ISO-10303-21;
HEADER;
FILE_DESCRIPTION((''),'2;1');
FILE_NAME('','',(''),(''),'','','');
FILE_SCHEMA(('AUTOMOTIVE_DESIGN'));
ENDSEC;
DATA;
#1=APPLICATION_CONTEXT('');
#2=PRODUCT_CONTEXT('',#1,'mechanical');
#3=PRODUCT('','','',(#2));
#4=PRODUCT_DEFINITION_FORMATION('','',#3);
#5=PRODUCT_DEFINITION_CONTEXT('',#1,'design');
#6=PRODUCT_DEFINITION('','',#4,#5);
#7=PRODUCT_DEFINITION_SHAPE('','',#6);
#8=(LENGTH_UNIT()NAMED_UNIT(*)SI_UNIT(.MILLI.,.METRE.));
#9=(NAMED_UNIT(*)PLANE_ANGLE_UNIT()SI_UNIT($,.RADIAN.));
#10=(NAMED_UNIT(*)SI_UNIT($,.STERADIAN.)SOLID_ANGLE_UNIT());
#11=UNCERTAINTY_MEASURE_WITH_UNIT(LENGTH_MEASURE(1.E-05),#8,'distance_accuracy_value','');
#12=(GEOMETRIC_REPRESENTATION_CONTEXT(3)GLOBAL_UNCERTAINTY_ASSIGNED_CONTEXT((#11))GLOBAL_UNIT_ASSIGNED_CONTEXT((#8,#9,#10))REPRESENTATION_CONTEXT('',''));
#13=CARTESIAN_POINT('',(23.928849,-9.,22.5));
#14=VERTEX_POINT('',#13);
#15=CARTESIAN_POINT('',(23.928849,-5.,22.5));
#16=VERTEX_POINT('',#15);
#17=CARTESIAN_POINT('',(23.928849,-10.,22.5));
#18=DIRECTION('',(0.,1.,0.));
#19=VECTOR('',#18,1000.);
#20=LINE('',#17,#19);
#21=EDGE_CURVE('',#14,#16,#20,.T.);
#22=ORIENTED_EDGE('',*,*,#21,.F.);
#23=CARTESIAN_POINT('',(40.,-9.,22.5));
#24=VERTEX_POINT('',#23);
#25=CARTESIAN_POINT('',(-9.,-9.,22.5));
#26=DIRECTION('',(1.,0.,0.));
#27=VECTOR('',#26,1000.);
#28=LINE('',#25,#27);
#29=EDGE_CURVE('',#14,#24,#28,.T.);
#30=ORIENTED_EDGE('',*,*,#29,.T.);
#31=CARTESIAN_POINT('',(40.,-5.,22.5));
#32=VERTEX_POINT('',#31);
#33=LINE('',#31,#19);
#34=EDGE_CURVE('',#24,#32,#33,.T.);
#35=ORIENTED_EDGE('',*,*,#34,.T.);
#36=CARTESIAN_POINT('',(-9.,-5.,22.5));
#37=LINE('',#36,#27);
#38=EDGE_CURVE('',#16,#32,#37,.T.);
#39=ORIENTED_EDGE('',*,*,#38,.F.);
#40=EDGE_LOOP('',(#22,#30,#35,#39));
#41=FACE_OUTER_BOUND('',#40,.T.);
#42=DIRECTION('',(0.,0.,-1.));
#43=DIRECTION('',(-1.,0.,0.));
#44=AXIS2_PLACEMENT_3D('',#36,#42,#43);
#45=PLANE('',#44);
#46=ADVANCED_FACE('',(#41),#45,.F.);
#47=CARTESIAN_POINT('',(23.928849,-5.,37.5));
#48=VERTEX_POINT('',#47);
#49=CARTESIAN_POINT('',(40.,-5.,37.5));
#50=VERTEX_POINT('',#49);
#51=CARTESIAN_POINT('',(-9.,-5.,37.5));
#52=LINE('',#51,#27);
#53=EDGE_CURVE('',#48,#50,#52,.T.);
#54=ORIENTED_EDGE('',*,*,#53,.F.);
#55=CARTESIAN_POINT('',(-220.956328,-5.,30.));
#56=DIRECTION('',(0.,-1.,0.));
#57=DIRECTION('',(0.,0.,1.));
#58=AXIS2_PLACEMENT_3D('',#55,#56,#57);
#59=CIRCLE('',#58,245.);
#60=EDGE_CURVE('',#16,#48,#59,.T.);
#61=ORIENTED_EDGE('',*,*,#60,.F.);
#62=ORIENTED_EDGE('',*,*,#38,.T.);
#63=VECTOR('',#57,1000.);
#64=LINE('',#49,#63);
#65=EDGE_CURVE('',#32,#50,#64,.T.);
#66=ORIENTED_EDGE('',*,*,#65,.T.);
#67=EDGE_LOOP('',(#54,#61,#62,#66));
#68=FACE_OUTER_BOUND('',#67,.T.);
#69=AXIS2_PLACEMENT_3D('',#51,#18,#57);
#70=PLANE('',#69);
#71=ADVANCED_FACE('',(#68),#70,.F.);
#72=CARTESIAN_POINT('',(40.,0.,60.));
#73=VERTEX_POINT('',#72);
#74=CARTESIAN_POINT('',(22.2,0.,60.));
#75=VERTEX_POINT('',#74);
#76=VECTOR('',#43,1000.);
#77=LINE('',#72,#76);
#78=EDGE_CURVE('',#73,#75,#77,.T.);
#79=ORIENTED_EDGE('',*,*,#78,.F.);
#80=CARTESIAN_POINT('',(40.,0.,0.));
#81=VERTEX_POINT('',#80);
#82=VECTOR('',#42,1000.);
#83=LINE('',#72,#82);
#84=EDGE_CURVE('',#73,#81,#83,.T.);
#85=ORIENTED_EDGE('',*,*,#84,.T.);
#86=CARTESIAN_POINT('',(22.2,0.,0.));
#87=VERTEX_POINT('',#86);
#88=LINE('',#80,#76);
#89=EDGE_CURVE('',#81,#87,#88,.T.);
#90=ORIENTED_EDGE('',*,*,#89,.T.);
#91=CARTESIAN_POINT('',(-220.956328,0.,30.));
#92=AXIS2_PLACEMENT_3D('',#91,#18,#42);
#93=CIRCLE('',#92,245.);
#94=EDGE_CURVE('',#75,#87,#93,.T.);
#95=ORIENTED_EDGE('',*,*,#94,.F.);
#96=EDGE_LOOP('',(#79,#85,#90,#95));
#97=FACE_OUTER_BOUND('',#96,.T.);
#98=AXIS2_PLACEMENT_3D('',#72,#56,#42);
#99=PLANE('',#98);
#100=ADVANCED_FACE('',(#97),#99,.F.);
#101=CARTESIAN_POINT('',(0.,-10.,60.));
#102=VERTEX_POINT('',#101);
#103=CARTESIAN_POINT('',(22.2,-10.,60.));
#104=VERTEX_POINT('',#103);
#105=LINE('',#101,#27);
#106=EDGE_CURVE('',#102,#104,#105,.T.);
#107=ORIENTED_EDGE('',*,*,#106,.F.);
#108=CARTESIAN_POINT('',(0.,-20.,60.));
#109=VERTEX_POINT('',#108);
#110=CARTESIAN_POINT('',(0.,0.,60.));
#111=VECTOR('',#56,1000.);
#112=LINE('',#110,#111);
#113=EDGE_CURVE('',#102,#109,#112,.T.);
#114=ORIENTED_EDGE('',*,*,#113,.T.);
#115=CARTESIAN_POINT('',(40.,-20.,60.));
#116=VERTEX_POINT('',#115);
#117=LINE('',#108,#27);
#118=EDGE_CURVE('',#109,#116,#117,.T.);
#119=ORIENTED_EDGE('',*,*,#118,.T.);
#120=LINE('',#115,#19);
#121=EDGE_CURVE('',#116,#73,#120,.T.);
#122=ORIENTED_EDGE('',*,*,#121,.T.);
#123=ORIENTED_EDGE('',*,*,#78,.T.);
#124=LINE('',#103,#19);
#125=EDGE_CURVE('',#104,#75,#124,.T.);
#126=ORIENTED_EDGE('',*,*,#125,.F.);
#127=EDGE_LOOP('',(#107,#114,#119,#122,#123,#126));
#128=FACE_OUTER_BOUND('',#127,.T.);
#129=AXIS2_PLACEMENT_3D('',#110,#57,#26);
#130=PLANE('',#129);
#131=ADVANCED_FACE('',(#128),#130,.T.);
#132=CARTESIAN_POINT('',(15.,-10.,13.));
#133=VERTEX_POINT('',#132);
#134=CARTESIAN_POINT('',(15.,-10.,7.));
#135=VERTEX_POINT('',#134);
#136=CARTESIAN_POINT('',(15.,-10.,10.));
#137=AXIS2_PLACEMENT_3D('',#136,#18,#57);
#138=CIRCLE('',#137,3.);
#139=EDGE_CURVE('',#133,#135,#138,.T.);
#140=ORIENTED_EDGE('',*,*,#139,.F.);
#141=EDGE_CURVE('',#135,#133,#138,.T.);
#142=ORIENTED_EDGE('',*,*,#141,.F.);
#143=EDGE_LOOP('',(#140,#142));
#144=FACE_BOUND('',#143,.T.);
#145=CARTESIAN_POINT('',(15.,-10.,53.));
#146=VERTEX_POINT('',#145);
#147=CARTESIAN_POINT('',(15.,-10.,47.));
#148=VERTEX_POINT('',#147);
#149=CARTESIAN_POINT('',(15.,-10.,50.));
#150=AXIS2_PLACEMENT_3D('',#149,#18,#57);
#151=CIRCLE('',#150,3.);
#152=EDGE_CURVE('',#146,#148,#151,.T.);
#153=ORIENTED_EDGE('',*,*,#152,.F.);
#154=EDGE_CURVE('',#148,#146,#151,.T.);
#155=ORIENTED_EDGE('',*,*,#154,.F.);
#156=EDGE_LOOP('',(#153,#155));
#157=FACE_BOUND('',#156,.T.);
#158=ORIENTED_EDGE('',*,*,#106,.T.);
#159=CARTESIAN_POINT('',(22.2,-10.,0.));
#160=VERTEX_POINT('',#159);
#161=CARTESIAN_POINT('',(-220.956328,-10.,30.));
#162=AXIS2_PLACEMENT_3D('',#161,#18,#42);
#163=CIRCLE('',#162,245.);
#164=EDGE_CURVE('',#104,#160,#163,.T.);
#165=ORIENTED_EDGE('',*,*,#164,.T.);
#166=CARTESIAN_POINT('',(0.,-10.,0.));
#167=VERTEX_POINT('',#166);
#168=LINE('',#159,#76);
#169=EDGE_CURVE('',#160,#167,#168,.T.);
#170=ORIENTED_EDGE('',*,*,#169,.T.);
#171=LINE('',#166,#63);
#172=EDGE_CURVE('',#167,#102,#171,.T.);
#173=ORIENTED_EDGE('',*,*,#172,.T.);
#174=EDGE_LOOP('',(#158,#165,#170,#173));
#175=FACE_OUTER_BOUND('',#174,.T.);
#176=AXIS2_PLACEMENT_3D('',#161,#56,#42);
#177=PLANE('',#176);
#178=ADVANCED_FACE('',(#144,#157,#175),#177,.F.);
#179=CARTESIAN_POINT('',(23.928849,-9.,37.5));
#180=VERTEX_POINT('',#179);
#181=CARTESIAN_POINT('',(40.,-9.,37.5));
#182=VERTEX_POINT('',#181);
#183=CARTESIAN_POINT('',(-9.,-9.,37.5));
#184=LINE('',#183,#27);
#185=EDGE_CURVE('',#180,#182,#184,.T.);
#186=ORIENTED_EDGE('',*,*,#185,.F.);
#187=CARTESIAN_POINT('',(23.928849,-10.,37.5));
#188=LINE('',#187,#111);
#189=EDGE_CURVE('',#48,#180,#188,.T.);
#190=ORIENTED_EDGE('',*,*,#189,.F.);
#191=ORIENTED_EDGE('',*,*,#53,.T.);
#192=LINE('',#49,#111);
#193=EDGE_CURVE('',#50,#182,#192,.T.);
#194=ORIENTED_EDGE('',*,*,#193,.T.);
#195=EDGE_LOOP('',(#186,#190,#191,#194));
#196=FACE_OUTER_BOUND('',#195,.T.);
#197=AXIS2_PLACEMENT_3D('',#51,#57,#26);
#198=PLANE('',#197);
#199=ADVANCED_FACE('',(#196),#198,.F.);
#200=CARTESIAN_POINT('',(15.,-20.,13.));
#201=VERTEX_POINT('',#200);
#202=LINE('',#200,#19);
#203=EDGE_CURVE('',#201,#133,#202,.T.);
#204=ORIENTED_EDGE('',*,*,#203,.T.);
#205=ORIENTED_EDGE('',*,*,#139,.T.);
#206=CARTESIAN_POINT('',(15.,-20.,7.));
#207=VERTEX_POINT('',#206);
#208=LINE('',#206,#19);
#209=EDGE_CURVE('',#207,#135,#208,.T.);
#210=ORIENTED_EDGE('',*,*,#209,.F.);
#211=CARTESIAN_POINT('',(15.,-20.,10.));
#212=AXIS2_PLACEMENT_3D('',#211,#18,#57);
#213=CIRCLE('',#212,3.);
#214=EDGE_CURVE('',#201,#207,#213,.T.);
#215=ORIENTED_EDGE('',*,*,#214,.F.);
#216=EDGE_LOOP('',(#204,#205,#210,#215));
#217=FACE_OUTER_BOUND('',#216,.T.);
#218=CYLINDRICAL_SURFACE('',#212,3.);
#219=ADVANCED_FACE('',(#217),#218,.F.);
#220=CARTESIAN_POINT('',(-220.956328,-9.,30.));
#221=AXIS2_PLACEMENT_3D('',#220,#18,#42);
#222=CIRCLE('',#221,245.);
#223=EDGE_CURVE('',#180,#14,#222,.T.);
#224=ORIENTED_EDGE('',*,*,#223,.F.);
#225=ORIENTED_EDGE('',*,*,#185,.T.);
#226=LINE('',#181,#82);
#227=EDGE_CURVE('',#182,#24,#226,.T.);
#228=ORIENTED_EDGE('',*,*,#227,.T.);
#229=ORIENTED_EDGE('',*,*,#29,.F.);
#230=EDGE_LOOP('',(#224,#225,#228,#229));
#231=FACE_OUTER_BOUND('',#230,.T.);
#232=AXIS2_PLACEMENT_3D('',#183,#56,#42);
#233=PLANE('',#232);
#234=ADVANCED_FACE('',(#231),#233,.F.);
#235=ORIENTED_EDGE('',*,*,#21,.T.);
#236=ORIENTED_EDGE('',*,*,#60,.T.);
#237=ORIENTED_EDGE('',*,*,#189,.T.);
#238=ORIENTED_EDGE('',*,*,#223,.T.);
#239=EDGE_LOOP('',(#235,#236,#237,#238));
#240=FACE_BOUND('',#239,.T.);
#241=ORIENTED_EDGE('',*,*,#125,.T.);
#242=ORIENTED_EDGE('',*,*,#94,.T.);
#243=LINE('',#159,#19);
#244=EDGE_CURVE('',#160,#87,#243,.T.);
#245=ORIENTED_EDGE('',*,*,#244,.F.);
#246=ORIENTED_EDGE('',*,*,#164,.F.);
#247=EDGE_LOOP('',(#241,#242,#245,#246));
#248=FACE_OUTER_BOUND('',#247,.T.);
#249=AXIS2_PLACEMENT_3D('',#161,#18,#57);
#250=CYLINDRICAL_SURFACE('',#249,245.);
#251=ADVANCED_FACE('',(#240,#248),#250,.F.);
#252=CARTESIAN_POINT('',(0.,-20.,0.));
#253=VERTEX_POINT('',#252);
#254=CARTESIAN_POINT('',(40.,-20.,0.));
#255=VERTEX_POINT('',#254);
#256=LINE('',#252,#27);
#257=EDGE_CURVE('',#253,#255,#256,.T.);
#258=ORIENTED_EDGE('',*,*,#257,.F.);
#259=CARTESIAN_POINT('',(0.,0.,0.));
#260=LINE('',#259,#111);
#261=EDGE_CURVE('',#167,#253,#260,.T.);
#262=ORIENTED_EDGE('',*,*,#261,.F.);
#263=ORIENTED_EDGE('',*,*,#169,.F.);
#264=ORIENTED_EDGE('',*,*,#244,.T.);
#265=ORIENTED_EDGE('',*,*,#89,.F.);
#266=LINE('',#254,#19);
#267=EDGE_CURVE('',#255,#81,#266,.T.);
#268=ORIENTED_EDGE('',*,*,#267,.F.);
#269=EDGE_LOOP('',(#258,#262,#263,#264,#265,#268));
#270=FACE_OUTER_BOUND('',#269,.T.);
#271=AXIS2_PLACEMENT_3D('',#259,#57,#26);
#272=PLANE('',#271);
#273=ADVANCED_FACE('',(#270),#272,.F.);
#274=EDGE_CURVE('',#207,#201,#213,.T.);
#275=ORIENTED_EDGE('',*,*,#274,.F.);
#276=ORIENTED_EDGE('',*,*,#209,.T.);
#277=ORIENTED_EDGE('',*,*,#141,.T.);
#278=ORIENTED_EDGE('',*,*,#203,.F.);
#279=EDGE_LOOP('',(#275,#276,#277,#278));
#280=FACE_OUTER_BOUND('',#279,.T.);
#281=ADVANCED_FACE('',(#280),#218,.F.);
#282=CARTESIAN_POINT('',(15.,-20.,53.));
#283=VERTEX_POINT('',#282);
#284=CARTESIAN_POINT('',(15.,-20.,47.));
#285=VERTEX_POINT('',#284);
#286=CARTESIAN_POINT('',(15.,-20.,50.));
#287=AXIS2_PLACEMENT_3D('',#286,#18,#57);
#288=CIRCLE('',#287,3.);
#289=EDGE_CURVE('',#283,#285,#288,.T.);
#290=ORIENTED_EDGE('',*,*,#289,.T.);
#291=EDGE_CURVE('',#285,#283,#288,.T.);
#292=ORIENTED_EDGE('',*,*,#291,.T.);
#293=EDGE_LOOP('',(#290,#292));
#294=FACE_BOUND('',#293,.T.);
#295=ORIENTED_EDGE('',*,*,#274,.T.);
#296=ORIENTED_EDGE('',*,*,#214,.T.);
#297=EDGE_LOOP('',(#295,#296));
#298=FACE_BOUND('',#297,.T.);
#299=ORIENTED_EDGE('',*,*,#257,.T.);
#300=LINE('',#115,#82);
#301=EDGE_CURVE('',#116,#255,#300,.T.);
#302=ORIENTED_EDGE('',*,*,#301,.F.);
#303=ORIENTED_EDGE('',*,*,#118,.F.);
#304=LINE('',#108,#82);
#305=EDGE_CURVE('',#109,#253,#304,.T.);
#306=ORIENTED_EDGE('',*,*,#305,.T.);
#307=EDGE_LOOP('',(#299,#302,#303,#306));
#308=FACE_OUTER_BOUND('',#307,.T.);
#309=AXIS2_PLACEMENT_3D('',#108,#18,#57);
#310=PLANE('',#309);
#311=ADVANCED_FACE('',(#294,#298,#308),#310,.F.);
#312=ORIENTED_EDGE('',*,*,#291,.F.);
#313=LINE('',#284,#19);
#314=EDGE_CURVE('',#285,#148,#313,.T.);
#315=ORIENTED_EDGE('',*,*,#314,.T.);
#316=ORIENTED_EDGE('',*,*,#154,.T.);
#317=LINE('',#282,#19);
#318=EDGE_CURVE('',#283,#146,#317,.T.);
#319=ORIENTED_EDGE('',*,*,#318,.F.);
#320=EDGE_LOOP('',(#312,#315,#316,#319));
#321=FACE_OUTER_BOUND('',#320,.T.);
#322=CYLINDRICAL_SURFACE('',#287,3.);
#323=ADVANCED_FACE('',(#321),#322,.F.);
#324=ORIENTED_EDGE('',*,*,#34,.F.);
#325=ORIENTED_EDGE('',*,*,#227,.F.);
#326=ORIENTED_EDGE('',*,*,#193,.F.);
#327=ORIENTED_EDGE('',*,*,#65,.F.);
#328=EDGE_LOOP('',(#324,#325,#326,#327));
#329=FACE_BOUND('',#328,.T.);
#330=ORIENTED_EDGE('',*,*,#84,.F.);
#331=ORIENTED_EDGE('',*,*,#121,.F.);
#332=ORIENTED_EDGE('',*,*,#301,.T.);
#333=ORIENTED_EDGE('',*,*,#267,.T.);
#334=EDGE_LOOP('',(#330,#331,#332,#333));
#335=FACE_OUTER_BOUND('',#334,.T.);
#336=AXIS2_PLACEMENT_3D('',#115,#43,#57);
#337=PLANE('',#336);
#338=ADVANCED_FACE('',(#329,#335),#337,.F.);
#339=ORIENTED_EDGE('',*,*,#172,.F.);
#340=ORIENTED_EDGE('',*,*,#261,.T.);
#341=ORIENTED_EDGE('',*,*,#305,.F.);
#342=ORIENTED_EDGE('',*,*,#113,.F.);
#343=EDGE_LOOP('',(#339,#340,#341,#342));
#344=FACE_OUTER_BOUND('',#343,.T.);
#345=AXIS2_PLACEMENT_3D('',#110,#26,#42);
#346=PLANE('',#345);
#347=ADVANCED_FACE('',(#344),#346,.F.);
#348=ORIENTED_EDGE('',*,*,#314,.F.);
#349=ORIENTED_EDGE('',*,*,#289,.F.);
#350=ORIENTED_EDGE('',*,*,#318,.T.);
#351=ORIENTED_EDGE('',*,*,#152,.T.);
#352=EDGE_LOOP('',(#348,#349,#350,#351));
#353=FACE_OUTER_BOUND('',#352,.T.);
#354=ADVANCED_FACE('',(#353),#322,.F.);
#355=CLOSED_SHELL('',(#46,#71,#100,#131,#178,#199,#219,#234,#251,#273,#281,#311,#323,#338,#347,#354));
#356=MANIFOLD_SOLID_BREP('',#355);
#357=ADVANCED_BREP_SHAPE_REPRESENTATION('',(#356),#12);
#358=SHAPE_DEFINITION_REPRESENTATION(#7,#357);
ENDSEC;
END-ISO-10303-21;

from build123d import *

# Parameters (mm, degrees)
SKETCH1_W           = 40
SKETCH1_H           = 20
BOSS_EXTRUDE1_DEPTH = 60
CUT_EXTRUDE1_DEPTH  = 10
SKETCH3_R           = 3
CUT_EXTRUDE2_DEPTH  = 10
SKETCH4_W           = 15
SKETCH4_H           = 4
CUT_EXTRUDE3_DEPTH  = 49


with BuildPart() as part:
    # Sketch1 → Boss-Extrude1 (new body)
    with BuildSketch(Plane.XY):
        with Locations((20, -10)):
            Rectangle(SKETCH1_W, SKETCH1_H)
    extrude(amount=BOSS_EXTRUDE1_DEPTH)

    # Sketch2 → Cut-Extrude1 (cut)
    with BuildSketch(Plane(origin=(0, 0, 0), x_dir=(1, 0, 0), z_dir=(0, 1, 0))):
        with BuildLine():
            Line((22.2, 0), (0, 0))
            Line((0, 0), (0, -60))
            Line((0, -60), (22.2, -60))
            ThreePointArc((22.2, -60), (24.043671684, -30), (22.2, 0))
        make_face()
    extrude(amount=-CUT_EXTRUDE1_DEPTH, mode=Mode.SUBTRACT)

    # Sketch3 → Cut-Extrude2 (cut)
    with BuildSketch(Plane(origin=(0, -10, 0), x_dir=(1, 0, 0), z_dir=(0, 1, 0))):
        with Locations(Location((15, -10, 0), (0, 0, 270))):
            Circle(SKETCH3_R)
        with Locations(Location((15, -50, 0), (0, 0, 270))):
            Circle(SKETCH3_R)
    extrude(amount=-CUT_EXTRUDE2_DEPTH, mode=Mode.SUBTRACT)

    # Sketch4 → Cut-Extrude3 (cut)
    with BuildSketch(Plane(origin=(40, 0, 0), x_dir=(0, 0, -1), z_dir=(1, 0, 0))):
        with Locations((-30, -7)):
            Rectangle(SKETCH4_W, SKETCH4_H)
    extrude(amount=-CUT_EXTRUDE3_DEPTH, mode=Mode.SUBTRACT)


solid = part.part
